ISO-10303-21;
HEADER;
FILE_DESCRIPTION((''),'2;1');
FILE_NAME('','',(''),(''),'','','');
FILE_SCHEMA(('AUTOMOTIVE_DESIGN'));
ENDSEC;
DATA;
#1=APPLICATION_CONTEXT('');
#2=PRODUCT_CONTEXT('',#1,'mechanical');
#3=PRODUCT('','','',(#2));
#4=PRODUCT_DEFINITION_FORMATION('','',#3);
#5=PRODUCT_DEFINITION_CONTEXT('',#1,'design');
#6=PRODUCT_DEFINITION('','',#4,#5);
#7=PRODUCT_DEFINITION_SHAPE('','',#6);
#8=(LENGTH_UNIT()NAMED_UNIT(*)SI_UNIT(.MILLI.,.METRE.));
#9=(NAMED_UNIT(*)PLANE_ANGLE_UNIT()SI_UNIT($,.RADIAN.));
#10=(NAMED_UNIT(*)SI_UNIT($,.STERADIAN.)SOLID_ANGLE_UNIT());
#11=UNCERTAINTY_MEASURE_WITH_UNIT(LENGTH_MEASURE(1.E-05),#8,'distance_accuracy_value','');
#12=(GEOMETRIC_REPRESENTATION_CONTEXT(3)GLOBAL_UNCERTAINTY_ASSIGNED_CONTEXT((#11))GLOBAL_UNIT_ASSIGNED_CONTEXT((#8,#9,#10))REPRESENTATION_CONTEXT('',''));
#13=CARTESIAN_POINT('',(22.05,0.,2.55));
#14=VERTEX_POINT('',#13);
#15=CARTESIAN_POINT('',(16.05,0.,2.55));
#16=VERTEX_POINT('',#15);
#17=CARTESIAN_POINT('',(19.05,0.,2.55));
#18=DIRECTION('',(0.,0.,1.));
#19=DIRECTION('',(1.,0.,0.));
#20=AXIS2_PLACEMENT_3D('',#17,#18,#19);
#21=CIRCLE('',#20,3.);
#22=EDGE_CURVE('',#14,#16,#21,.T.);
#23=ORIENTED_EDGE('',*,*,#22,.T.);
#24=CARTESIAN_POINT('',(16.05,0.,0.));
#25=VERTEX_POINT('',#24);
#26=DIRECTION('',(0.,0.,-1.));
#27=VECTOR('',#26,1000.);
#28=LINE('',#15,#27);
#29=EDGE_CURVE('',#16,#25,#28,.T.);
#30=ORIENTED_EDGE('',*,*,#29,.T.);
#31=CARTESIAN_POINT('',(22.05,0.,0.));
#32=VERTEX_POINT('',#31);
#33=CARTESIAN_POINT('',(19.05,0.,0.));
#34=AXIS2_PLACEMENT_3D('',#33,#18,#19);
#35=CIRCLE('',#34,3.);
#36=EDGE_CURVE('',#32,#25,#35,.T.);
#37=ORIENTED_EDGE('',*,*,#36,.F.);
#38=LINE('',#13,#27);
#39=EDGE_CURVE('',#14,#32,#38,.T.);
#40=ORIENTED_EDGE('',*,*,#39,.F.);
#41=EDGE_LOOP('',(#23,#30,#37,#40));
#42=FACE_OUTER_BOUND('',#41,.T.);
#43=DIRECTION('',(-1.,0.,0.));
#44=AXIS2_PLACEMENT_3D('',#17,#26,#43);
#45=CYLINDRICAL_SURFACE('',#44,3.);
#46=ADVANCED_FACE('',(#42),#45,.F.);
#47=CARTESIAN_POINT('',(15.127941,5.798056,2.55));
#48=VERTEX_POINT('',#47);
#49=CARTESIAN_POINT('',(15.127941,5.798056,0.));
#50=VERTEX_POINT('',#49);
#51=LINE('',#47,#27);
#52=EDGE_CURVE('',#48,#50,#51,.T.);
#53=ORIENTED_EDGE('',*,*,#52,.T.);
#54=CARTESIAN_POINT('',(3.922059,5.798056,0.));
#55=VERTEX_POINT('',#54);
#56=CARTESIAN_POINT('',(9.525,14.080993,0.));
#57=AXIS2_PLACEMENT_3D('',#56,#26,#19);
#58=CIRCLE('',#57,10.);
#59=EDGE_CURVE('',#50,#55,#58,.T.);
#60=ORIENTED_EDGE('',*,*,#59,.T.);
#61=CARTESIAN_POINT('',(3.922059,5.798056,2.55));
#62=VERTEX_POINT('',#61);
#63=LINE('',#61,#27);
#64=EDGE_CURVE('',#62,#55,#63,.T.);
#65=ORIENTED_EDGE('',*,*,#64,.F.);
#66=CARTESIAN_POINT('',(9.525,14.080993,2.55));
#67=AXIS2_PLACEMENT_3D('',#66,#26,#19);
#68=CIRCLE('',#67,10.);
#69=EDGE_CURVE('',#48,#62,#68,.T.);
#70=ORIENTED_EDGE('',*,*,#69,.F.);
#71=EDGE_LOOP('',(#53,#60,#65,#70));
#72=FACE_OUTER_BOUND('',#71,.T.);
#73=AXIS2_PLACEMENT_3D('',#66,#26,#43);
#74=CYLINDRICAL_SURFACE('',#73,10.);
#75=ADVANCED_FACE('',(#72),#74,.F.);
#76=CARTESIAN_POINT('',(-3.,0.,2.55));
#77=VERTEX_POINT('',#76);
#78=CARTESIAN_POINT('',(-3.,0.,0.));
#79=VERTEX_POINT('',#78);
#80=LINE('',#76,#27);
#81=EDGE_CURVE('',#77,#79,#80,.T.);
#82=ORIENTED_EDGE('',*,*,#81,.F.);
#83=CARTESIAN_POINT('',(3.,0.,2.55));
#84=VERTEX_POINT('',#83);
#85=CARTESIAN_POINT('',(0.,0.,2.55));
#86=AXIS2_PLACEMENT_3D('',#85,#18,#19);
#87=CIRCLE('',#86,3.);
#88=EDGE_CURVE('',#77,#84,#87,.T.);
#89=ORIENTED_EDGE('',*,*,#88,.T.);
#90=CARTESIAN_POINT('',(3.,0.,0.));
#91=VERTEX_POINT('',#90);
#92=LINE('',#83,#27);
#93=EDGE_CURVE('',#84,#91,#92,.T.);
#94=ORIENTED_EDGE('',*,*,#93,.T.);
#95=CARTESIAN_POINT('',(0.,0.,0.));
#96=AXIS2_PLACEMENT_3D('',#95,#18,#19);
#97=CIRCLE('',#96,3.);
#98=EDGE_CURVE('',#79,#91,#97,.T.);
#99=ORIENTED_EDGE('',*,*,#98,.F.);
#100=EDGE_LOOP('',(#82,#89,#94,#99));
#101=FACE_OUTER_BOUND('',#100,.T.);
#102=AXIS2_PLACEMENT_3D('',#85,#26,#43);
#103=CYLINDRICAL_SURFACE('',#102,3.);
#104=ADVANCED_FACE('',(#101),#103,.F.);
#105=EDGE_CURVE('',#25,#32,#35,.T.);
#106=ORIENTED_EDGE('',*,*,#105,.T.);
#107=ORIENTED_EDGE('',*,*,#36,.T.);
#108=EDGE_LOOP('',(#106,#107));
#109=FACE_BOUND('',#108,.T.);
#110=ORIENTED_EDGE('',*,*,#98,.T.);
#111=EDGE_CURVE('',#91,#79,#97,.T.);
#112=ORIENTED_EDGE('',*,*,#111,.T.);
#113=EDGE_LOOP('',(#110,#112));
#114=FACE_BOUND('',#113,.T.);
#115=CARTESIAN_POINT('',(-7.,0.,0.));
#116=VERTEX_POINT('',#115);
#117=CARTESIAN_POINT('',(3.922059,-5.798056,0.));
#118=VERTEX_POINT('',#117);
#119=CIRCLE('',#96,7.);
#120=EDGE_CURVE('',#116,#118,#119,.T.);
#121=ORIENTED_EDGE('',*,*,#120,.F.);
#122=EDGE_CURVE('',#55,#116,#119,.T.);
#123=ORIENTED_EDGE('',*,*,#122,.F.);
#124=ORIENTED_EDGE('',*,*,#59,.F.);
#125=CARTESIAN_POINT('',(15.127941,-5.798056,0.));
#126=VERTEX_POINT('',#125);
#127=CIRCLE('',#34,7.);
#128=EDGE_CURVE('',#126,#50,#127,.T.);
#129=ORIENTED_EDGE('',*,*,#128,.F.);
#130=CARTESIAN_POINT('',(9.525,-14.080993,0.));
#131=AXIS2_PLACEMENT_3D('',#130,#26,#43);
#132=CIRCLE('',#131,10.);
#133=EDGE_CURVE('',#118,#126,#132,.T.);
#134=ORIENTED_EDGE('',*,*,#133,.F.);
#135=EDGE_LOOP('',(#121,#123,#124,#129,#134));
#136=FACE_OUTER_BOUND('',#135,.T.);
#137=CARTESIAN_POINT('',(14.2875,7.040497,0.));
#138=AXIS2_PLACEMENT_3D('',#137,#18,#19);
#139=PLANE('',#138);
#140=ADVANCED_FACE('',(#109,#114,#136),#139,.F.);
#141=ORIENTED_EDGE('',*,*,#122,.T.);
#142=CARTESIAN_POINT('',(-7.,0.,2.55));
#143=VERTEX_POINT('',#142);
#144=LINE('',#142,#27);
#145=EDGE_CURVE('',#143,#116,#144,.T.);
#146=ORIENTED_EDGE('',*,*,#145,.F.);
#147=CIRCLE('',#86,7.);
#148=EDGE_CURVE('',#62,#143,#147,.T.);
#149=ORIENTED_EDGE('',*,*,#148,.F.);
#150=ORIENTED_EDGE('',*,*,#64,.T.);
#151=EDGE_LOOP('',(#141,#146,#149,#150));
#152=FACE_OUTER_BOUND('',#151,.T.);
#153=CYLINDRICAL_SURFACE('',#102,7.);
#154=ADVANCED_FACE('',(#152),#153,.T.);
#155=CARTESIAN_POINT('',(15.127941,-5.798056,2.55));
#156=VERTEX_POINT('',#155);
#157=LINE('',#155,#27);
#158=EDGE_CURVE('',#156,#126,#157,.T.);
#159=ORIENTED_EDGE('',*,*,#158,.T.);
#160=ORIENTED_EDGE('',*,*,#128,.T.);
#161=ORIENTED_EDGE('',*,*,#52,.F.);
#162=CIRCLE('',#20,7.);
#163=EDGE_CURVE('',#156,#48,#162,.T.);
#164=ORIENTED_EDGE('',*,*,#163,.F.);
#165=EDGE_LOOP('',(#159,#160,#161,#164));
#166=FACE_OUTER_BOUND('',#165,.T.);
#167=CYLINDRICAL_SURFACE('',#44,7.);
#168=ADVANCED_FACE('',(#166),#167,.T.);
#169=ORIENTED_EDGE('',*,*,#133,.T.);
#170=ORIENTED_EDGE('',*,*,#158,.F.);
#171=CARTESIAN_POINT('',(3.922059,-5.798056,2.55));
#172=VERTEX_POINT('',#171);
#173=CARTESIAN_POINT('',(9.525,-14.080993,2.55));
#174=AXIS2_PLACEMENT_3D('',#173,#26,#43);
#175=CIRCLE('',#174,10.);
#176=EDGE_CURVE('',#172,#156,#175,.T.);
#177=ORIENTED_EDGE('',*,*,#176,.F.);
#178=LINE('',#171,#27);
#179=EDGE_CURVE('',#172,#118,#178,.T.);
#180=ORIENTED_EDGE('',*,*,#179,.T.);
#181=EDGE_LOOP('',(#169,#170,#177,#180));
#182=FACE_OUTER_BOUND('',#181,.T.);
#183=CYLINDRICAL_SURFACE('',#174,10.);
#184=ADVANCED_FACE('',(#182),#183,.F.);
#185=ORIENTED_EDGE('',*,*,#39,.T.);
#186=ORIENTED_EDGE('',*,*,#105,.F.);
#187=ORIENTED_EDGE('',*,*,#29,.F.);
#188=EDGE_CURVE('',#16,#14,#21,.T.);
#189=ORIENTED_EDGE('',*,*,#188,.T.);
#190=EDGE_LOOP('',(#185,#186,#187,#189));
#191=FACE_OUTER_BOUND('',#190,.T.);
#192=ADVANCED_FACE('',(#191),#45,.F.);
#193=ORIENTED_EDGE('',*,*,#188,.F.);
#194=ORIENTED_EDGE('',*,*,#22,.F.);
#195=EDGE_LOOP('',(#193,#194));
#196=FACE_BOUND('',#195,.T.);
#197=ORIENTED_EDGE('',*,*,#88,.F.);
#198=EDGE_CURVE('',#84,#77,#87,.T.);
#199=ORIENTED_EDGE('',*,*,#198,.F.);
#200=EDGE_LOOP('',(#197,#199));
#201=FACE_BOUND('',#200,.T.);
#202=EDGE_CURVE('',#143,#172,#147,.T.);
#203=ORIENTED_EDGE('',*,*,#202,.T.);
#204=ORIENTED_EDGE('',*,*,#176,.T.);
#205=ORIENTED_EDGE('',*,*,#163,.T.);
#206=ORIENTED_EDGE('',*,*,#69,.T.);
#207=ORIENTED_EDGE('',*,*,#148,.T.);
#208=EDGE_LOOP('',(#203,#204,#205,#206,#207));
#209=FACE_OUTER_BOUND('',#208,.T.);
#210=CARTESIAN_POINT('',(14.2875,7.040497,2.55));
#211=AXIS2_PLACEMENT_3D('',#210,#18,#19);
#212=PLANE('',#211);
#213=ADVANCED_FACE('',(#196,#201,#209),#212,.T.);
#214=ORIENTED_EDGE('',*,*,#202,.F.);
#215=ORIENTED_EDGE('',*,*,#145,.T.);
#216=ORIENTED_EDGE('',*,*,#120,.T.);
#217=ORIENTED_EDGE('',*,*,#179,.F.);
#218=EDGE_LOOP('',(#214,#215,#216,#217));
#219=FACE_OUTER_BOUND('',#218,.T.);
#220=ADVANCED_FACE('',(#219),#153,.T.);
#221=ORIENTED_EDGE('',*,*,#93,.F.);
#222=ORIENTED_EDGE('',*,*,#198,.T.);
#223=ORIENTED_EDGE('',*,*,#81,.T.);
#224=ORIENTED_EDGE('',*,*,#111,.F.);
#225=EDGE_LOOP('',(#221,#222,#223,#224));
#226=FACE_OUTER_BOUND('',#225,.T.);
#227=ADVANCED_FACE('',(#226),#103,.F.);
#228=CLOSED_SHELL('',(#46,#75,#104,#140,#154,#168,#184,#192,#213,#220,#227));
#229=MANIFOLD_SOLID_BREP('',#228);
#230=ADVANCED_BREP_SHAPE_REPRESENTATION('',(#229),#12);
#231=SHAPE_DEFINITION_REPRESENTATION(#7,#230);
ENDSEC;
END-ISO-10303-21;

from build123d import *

# Parameters (mm, degrees)
SKETCH1_R           = 3
BOSS_EXTRUDE1_DEPTH = 2.55


with BuildPart() as part:
    # Sketch1 → Boss-Extrude1 (new body)
    with BuildSketch(Plane.XY):
        with BuildLine():
            ThreePointArc((3.922058824, 5.798056104), (-7, 0), (3.922058824, -5.798056104))
            ThreePointArc((3.922058824, -5.798056104), (9.525, -4.080993395), (15.127941176, -5.798056104))
            ThreePointArc((15.127941176, -5.798056104), (26.05, 0), (15.127941176, 5.798056104))
            ThreePointArc((15.127941176, 5.798056104), (9.525, 4.080993395), (3.922058824, 5.798056104))
        make_face()
        Circle(SKETCH1_R, mode=Mode.SUBTRACT)
        with Locations((19.05, 0)):
            Circle(SKETCH1_R, mode=Mode.SUBTRACT)
    extrude(amount=BOSS_EXTRUDE1_DEPTH)


solid = part.part
